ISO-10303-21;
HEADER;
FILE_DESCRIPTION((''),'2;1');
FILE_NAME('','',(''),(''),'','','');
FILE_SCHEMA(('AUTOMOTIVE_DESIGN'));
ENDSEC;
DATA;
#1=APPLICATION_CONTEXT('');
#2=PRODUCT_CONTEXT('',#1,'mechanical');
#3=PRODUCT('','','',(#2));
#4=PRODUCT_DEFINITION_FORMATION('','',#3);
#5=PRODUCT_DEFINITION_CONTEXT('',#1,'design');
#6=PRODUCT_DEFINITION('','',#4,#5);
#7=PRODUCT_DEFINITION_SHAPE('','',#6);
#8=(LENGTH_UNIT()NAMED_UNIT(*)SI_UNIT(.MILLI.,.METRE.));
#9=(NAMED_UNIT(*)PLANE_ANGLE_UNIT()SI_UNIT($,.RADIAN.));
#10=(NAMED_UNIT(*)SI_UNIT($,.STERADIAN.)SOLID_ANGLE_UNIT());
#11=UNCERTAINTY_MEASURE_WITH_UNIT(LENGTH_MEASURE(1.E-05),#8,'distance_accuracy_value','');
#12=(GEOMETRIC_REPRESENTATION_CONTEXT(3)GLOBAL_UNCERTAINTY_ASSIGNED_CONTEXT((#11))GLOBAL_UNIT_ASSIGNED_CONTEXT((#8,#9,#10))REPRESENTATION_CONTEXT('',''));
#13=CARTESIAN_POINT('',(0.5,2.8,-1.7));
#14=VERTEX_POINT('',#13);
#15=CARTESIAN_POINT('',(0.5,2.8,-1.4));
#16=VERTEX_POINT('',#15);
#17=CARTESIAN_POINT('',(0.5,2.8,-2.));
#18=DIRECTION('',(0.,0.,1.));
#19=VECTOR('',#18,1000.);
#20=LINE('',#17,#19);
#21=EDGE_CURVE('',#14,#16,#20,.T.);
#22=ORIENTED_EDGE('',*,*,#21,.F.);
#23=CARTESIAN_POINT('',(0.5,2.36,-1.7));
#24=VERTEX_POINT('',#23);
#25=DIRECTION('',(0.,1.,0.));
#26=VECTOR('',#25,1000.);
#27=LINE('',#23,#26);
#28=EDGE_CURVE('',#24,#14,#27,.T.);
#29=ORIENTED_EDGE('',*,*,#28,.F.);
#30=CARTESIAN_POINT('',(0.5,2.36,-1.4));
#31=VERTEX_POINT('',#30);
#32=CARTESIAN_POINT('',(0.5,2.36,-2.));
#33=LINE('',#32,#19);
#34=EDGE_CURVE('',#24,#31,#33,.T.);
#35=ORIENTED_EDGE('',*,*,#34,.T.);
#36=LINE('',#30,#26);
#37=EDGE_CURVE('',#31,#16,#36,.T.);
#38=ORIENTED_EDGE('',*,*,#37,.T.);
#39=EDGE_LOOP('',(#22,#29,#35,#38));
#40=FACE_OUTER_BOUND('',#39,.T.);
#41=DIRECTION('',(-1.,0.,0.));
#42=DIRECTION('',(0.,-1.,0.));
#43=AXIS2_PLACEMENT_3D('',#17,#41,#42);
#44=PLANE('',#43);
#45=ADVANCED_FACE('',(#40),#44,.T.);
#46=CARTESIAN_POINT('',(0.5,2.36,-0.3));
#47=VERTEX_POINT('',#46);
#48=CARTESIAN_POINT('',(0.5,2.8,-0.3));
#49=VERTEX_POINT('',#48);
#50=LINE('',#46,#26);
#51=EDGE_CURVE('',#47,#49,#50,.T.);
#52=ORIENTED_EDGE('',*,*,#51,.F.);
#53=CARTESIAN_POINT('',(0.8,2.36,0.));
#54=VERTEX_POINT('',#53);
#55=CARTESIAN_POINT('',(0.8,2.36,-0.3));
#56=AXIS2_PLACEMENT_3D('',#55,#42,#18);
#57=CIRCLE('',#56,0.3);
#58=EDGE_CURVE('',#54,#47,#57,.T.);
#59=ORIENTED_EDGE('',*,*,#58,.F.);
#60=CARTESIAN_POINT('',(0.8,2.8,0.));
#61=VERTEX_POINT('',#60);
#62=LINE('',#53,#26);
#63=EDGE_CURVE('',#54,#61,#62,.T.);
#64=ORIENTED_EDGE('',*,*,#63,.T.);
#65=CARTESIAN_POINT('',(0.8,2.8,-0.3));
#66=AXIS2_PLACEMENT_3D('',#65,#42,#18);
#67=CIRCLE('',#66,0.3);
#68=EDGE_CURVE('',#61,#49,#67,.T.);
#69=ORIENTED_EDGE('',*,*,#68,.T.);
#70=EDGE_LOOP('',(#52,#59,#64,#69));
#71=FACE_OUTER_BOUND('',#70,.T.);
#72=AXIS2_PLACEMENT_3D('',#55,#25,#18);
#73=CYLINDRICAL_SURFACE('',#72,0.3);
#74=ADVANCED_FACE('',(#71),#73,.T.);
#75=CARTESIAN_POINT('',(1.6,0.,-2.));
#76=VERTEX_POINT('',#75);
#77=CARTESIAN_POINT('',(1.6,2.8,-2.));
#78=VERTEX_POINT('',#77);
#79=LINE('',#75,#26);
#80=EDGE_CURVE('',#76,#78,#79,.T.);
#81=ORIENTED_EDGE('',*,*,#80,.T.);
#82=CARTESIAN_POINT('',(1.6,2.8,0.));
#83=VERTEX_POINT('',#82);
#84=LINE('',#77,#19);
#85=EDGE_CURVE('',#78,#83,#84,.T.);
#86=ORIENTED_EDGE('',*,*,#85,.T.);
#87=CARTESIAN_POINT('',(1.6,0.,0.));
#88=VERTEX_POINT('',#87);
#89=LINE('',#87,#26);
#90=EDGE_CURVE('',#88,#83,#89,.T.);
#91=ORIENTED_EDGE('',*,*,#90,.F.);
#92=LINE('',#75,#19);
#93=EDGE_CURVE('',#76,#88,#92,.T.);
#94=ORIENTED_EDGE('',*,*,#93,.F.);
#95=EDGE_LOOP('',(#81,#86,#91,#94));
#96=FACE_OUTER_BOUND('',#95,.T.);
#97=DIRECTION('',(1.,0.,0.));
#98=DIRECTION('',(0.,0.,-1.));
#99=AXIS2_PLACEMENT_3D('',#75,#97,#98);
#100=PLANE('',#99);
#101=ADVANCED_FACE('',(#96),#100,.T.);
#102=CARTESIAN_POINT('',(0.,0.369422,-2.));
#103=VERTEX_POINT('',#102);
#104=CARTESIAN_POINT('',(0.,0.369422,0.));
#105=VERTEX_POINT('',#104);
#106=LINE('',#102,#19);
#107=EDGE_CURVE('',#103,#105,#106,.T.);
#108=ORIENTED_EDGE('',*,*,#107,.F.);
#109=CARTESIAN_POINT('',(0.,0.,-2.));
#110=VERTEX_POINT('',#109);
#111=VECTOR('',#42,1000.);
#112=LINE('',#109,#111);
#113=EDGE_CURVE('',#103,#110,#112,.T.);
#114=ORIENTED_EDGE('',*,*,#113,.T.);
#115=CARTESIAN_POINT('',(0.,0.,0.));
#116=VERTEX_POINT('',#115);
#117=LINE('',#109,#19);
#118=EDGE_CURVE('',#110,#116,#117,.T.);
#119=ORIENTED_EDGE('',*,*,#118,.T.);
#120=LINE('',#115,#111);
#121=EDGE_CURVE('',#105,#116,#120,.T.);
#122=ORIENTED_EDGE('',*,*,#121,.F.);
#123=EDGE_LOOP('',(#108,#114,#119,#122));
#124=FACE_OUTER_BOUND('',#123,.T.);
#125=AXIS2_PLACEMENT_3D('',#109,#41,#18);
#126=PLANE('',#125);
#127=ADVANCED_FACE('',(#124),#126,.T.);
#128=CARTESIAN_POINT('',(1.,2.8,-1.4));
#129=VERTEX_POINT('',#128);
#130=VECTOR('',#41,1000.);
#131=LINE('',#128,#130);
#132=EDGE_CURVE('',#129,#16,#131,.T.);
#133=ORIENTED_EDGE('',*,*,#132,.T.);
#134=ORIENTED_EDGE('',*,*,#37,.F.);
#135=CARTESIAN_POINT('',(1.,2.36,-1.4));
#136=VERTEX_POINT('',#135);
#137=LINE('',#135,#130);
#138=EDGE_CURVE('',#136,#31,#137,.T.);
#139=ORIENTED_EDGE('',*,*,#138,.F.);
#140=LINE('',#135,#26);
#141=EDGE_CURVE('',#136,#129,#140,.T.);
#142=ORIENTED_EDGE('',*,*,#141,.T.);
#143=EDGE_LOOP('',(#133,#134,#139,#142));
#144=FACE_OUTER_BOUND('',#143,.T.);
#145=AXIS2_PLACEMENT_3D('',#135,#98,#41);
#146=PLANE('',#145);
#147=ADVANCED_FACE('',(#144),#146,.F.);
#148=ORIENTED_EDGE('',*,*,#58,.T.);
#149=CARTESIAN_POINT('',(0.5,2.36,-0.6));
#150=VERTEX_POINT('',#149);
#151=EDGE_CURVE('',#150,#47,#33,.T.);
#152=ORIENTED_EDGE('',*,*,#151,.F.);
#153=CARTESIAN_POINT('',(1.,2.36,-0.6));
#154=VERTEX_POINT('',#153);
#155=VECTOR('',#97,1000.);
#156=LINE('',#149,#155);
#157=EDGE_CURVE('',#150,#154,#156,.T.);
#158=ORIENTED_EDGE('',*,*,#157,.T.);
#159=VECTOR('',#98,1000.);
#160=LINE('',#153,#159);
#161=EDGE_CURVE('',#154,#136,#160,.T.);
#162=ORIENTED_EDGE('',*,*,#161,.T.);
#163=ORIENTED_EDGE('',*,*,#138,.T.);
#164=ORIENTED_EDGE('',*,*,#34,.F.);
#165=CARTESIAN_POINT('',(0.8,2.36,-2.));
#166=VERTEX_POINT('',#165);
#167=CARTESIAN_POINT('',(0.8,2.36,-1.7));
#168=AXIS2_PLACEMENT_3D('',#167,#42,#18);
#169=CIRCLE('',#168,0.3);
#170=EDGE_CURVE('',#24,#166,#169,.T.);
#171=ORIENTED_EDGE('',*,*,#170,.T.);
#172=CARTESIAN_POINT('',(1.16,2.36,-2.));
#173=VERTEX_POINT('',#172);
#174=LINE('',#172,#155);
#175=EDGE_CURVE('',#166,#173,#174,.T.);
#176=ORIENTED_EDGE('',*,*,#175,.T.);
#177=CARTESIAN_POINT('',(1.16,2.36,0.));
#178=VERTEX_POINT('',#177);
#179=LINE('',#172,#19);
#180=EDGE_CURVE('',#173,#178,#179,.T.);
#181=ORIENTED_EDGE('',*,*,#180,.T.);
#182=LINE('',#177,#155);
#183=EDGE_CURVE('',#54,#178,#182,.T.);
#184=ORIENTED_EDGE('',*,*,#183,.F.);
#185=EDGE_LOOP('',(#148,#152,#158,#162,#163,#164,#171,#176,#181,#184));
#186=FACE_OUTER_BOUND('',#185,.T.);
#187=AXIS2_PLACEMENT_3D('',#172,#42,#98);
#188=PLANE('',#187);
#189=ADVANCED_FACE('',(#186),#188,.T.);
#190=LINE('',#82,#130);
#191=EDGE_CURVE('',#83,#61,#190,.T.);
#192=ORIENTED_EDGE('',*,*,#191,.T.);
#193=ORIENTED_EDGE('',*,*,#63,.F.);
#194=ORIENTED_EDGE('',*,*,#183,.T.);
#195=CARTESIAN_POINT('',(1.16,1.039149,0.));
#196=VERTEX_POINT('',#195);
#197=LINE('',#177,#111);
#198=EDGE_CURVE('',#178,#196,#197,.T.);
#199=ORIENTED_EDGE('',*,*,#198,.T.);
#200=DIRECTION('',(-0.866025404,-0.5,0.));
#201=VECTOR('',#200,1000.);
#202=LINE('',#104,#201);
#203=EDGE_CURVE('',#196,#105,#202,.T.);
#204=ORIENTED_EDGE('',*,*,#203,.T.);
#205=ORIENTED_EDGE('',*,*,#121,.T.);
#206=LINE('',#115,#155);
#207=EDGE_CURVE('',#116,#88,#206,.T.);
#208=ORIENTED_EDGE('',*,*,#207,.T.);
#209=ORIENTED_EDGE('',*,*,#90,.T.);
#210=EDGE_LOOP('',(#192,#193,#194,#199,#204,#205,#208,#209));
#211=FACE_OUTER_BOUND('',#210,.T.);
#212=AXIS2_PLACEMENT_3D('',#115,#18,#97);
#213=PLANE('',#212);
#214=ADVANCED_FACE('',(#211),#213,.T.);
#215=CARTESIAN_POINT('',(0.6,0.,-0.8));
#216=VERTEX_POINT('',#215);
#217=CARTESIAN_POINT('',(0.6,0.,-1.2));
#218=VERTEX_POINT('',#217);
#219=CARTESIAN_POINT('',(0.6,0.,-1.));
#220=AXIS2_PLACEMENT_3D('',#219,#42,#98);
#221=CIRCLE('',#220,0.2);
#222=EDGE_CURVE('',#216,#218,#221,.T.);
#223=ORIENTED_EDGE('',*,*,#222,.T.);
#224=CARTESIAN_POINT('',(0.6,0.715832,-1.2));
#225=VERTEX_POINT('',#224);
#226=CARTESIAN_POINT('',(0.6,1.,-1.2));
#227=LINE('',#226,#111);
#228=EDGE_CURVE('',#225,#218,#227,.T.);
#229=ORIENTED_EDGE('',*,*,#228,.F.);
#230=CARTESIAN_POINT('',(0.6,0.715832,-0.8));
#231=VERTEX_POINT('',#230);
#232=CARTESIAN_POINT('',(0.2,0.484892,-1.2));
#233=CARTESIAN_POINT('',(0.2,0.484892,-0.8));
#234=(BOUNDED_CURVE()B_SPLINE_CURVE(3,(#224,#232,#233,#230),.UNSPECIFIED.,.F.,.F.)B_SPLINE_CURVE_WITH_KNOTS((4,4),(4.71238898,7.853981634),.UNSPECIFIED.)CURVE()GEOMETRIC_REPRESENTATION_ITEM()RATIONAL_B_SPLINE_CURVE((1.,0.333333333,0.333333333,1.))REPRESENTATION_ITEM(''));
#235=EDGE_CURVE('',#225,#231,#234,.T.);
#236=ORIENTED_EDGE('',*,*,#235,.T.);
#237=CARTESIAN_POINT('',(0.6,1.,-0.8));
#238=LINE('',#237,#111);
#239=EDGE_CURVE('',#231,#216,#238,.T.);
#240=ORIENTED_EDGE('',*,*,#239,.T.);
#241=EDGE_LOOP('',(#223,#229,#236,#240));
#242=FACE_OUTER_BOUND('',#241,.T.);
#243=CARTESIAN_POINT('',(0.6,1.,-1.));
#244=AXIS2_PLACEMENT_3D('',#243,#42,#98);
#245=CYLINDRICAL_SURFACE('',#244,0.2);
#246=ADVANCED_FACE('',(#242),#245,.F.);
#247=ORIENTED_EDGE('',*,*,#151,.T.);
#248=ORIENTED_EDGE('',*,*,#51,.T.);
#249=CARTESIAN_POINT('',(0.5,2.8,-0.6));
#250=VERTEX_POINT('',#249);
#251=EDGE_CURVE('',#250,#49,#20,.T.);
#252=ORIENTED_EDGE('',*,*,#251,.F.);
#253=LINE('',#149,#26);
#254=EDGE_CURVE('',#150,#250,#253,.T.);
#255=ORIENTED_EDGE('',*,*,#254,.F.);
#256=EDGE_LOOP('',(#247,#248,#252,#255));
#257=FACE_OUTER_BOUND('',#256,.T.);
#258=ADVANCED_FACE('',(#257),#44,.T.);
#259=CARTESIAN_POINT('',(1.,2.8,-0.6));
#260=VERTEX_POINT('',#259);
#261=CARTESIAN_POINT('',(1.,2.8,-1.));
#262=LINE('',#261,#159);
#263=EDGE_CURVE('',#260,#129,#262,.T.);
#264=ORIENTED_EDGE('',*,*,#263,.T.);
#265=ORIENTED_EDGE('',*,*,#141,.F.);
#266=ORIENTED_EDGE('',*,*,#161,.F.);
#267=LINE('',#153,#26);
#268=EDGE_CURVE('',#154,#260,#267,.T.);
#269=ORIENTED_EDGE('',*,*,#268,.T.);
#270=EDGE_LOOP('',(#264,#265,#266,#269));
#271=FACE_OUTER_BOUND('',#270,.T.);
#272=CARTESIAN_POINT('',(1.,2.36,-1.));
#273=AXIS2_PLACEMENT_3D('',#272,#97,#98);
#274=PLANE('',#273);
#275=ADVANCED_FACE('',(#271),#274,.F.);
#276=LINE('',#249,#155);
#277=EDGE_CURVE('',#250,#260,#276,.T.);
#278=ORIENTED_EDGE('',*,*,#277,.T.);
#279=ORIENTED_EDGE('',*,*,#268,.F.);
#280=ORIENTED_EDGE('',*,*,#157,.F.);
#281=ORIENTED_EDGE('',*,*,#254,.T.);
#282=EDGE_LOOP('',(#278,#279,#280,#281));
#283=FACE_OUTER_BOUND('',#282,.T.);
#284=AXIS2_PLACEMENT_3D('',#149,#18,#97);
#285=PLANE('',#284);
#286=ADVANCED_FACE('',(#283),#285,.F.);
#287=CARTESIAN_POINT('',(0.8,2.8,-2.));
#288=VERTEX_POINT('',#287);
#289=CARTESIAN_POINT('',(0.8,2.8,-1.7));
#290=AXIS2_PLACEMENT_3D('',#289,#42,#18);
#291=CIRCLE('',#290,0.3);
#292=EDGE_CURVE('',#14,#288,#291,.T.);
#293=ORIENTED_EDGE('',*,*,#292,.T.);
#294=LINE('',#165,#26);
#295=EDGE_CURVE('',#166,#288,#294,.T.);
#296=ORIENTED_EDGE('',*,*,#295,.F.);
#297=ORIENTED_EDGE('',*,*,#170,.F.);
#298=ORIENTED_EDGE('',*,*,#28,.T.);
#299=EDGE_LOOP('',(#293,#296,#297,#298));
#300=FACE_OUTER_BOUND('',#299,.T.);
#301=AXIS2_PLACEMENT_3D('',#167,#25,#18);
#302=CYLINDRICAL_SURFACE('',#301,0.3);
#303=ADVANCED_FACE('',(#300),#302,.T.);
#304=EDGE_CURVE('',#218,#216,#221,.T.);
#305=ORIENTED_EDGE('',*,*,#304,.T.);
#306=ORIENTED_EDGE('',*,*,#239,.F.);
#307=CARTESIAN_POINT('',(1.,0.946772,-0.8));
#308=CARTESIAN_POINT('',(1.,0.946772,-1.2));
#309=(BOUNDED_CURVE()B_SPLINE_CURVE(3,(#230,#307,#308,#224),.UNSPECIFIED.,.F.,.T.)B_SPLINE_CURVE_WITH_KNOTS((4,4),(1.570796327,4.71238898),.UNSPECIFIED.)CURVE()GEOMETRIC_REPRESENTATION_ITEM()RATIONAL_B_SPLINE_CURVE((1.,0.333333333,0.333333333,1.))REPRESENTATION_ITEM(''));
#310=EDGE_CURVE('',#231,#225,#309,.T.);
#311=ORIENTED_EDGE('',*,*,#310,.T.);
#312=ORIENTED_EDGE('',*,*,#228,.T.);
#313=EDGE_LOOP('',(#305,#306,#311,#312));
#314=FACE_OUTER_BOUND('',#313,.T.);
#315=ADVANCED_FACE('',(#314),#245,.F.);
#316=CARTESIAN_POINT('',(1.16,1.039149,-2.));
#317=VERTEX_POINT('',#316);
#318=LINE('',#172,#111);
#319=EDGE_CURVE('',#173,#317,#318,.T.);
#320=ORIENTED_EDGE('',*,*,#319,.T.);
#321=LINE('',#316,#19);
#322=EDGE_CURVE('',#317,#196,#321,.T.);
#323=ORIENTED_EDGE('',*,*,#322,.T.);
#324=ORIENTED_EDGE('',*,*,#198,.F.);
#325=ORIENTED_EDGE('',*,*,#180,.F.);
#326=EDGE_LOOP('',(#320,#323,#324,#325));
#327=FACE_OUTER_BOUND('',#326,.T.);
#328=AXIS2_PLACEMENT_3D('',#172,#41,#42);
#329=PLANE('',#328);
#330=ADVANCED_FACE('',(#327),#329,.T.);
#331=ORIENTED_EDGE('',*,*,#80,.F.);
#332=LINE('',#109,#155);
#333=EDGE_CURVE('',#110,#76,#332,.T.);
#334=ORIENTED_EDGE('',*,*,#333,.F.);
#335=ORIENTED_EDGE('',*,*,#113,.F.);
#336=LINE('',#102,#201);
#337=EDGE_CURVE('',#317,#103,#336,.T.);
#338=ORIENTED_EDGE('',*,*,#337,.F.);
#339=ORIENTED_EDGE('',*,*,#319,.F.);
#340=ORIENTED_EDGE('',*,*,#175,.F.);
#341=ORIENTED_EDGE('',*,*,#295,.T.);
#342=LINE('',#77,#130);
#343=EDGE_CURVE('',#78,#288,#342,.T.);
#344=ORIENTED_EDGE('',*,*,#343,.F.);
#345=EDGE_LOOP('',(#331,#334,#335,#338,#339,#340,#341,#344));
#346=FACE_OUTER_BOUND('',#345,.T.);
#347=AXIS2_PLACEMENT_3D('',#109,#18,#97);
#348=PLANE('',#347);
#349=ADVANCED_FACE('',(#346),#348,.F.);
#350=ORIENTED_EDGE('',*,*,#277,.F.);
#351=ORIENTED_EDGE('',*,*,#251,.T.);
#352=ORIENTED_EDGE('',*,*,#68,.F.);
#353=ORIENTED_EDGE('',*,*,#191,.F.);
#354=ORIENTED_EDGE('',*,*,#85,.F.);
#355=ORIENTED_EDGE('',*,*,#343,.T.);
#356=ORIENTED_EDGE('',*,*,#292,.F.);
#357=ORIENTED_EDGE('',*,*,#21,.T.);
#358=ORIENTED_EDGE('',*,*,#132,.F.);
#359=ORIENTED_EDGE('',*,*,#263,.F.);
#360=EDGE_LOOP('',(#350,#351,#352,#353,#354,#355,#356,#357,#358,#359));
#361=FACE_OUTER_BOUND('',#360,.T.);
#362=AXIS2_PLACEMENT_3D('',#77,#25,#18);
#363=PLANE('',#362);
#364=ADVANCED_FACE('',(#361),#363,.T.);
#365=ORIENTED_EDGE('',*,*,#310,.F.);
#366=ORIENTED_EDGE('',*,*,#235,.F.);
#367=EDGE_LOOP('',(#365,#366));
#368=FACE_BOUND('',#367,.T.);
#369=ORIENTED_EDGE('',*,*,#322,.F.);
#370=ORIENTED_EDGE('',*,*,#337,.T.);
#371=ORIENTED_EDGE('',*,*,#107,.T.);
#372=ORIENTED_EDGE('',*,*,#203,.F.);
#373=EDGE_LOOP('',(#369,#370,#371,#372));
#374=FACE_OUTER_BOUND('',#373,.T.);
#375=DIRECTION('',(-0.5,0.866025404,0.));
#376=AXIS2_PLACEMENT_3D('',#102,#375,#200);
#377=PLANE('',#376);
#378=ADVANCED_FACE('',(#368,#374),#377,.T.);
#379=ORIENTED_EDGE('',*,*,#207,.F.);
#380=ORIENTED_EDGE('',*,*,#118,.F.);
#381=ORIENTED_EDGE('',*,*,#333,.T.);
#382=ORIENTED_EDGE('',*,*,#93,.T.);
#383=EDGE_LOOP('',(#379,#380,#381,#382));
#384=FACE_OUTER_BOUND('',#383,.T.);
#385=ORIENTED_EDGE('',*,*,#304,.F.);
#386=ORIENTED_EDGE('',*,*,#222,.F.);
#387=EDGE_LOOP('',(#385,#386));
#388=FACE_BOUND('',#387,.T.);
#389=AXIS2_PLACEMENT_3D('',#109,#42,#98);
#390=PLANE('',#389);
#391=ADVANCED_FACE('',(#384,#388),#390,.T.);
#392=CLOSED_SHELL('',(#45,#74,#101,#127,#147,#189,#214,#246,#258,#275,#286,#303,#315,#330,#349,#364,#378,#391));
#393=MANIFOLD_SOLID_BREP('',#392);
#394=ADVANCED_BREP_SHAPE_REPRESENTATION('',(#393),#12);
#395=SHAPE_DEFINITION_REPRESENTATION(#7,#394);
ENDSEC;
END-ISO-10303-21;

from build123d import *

# Parameters (mm, degrees)
C_BRACKET_BODY_DEPTH         = 2
RECESS_CUT_A_0_44_DEEP_DEPTH = 0.44
RECESS_CUT_B_0_44_DEEP_DEPTH = 0.44
HOLE_SKETCH_R                = 0.2
HOLE_0_4_X_1_DEEP_DEPTH      = 1


with BuildPart() as part:
    # C-Profile Sketch → C-Bracket Body (new body)
    with BuildSketch(Plane.XY):
        Polygon((0, 0), (1.6, 0), (1.6, 2.8), (0.5, 2.8), (0.5, 2.36), (1.16, 2.36), (1.16, 1.039148534), (0, 0.369422221), align=None)
    extrude(amount=-C_BRACKET_BODY_DEPTH)

    # Recess Cut A Sketch → Recess Cut A 0.44 Deep (cut)
    with BuildSketch(Plane(origin=(0, 2.8, 0), x_dir=(1, 0, 0), z_dir=(0, 1, 0))):
        with BuildLine():
            Line((0.5, 2), (0.8, 2))
            ThreePointArc((0.8, 2), (0.587867966, 1.912132034), (0.5, 1.7))
            Line((0.5, 1.7), (0.5, 2))
        make_face()
        with BuildLine():
            Line((0.5, 0), (0.8, 0))
            ThreePointArc((0.8, 0), (0.587867966, 0.087867966), (0.5, 0.3))
            Line((0.5, 0.3), (0.5, 0))
        make_face()
    extrude(amount=-RECESS_CUT_A_0_44_DEEP_DEPTH, mode=Mode.SUBTRACT)

    # Recess Cut B Sketch → Recess Cut B 0.44 Deep (cut)
    with BuildSketch(Plane(origin=(0, 2.8, 0), x_dir=(1, 0, 0), z_dir=(0, 1, 0))):
        Polygon((1, 1), (1, 1.4), (0.5, 1.4), (0.5, 0.6), (1, 0.6), align=None)
    extrude(amount=-RECESS_CUT_B_0_44_DEEP_DEPTH, mode=Mode.SUBTRACT)

    # Hole Sketch → Hole Ø0.4 x 1 Deep (cut)
    with BuildSketch(Plane.XZ):
        with Locations(Location((0.6, -1, 0), (0, 0, 270))):
            Circle(HOLE_SKETCH_R)
    extrude(amount=-HOLE_0_4_X_1_DEEP_DEPTH, mode=Mode.SUBTRACT)


solid = part.part
